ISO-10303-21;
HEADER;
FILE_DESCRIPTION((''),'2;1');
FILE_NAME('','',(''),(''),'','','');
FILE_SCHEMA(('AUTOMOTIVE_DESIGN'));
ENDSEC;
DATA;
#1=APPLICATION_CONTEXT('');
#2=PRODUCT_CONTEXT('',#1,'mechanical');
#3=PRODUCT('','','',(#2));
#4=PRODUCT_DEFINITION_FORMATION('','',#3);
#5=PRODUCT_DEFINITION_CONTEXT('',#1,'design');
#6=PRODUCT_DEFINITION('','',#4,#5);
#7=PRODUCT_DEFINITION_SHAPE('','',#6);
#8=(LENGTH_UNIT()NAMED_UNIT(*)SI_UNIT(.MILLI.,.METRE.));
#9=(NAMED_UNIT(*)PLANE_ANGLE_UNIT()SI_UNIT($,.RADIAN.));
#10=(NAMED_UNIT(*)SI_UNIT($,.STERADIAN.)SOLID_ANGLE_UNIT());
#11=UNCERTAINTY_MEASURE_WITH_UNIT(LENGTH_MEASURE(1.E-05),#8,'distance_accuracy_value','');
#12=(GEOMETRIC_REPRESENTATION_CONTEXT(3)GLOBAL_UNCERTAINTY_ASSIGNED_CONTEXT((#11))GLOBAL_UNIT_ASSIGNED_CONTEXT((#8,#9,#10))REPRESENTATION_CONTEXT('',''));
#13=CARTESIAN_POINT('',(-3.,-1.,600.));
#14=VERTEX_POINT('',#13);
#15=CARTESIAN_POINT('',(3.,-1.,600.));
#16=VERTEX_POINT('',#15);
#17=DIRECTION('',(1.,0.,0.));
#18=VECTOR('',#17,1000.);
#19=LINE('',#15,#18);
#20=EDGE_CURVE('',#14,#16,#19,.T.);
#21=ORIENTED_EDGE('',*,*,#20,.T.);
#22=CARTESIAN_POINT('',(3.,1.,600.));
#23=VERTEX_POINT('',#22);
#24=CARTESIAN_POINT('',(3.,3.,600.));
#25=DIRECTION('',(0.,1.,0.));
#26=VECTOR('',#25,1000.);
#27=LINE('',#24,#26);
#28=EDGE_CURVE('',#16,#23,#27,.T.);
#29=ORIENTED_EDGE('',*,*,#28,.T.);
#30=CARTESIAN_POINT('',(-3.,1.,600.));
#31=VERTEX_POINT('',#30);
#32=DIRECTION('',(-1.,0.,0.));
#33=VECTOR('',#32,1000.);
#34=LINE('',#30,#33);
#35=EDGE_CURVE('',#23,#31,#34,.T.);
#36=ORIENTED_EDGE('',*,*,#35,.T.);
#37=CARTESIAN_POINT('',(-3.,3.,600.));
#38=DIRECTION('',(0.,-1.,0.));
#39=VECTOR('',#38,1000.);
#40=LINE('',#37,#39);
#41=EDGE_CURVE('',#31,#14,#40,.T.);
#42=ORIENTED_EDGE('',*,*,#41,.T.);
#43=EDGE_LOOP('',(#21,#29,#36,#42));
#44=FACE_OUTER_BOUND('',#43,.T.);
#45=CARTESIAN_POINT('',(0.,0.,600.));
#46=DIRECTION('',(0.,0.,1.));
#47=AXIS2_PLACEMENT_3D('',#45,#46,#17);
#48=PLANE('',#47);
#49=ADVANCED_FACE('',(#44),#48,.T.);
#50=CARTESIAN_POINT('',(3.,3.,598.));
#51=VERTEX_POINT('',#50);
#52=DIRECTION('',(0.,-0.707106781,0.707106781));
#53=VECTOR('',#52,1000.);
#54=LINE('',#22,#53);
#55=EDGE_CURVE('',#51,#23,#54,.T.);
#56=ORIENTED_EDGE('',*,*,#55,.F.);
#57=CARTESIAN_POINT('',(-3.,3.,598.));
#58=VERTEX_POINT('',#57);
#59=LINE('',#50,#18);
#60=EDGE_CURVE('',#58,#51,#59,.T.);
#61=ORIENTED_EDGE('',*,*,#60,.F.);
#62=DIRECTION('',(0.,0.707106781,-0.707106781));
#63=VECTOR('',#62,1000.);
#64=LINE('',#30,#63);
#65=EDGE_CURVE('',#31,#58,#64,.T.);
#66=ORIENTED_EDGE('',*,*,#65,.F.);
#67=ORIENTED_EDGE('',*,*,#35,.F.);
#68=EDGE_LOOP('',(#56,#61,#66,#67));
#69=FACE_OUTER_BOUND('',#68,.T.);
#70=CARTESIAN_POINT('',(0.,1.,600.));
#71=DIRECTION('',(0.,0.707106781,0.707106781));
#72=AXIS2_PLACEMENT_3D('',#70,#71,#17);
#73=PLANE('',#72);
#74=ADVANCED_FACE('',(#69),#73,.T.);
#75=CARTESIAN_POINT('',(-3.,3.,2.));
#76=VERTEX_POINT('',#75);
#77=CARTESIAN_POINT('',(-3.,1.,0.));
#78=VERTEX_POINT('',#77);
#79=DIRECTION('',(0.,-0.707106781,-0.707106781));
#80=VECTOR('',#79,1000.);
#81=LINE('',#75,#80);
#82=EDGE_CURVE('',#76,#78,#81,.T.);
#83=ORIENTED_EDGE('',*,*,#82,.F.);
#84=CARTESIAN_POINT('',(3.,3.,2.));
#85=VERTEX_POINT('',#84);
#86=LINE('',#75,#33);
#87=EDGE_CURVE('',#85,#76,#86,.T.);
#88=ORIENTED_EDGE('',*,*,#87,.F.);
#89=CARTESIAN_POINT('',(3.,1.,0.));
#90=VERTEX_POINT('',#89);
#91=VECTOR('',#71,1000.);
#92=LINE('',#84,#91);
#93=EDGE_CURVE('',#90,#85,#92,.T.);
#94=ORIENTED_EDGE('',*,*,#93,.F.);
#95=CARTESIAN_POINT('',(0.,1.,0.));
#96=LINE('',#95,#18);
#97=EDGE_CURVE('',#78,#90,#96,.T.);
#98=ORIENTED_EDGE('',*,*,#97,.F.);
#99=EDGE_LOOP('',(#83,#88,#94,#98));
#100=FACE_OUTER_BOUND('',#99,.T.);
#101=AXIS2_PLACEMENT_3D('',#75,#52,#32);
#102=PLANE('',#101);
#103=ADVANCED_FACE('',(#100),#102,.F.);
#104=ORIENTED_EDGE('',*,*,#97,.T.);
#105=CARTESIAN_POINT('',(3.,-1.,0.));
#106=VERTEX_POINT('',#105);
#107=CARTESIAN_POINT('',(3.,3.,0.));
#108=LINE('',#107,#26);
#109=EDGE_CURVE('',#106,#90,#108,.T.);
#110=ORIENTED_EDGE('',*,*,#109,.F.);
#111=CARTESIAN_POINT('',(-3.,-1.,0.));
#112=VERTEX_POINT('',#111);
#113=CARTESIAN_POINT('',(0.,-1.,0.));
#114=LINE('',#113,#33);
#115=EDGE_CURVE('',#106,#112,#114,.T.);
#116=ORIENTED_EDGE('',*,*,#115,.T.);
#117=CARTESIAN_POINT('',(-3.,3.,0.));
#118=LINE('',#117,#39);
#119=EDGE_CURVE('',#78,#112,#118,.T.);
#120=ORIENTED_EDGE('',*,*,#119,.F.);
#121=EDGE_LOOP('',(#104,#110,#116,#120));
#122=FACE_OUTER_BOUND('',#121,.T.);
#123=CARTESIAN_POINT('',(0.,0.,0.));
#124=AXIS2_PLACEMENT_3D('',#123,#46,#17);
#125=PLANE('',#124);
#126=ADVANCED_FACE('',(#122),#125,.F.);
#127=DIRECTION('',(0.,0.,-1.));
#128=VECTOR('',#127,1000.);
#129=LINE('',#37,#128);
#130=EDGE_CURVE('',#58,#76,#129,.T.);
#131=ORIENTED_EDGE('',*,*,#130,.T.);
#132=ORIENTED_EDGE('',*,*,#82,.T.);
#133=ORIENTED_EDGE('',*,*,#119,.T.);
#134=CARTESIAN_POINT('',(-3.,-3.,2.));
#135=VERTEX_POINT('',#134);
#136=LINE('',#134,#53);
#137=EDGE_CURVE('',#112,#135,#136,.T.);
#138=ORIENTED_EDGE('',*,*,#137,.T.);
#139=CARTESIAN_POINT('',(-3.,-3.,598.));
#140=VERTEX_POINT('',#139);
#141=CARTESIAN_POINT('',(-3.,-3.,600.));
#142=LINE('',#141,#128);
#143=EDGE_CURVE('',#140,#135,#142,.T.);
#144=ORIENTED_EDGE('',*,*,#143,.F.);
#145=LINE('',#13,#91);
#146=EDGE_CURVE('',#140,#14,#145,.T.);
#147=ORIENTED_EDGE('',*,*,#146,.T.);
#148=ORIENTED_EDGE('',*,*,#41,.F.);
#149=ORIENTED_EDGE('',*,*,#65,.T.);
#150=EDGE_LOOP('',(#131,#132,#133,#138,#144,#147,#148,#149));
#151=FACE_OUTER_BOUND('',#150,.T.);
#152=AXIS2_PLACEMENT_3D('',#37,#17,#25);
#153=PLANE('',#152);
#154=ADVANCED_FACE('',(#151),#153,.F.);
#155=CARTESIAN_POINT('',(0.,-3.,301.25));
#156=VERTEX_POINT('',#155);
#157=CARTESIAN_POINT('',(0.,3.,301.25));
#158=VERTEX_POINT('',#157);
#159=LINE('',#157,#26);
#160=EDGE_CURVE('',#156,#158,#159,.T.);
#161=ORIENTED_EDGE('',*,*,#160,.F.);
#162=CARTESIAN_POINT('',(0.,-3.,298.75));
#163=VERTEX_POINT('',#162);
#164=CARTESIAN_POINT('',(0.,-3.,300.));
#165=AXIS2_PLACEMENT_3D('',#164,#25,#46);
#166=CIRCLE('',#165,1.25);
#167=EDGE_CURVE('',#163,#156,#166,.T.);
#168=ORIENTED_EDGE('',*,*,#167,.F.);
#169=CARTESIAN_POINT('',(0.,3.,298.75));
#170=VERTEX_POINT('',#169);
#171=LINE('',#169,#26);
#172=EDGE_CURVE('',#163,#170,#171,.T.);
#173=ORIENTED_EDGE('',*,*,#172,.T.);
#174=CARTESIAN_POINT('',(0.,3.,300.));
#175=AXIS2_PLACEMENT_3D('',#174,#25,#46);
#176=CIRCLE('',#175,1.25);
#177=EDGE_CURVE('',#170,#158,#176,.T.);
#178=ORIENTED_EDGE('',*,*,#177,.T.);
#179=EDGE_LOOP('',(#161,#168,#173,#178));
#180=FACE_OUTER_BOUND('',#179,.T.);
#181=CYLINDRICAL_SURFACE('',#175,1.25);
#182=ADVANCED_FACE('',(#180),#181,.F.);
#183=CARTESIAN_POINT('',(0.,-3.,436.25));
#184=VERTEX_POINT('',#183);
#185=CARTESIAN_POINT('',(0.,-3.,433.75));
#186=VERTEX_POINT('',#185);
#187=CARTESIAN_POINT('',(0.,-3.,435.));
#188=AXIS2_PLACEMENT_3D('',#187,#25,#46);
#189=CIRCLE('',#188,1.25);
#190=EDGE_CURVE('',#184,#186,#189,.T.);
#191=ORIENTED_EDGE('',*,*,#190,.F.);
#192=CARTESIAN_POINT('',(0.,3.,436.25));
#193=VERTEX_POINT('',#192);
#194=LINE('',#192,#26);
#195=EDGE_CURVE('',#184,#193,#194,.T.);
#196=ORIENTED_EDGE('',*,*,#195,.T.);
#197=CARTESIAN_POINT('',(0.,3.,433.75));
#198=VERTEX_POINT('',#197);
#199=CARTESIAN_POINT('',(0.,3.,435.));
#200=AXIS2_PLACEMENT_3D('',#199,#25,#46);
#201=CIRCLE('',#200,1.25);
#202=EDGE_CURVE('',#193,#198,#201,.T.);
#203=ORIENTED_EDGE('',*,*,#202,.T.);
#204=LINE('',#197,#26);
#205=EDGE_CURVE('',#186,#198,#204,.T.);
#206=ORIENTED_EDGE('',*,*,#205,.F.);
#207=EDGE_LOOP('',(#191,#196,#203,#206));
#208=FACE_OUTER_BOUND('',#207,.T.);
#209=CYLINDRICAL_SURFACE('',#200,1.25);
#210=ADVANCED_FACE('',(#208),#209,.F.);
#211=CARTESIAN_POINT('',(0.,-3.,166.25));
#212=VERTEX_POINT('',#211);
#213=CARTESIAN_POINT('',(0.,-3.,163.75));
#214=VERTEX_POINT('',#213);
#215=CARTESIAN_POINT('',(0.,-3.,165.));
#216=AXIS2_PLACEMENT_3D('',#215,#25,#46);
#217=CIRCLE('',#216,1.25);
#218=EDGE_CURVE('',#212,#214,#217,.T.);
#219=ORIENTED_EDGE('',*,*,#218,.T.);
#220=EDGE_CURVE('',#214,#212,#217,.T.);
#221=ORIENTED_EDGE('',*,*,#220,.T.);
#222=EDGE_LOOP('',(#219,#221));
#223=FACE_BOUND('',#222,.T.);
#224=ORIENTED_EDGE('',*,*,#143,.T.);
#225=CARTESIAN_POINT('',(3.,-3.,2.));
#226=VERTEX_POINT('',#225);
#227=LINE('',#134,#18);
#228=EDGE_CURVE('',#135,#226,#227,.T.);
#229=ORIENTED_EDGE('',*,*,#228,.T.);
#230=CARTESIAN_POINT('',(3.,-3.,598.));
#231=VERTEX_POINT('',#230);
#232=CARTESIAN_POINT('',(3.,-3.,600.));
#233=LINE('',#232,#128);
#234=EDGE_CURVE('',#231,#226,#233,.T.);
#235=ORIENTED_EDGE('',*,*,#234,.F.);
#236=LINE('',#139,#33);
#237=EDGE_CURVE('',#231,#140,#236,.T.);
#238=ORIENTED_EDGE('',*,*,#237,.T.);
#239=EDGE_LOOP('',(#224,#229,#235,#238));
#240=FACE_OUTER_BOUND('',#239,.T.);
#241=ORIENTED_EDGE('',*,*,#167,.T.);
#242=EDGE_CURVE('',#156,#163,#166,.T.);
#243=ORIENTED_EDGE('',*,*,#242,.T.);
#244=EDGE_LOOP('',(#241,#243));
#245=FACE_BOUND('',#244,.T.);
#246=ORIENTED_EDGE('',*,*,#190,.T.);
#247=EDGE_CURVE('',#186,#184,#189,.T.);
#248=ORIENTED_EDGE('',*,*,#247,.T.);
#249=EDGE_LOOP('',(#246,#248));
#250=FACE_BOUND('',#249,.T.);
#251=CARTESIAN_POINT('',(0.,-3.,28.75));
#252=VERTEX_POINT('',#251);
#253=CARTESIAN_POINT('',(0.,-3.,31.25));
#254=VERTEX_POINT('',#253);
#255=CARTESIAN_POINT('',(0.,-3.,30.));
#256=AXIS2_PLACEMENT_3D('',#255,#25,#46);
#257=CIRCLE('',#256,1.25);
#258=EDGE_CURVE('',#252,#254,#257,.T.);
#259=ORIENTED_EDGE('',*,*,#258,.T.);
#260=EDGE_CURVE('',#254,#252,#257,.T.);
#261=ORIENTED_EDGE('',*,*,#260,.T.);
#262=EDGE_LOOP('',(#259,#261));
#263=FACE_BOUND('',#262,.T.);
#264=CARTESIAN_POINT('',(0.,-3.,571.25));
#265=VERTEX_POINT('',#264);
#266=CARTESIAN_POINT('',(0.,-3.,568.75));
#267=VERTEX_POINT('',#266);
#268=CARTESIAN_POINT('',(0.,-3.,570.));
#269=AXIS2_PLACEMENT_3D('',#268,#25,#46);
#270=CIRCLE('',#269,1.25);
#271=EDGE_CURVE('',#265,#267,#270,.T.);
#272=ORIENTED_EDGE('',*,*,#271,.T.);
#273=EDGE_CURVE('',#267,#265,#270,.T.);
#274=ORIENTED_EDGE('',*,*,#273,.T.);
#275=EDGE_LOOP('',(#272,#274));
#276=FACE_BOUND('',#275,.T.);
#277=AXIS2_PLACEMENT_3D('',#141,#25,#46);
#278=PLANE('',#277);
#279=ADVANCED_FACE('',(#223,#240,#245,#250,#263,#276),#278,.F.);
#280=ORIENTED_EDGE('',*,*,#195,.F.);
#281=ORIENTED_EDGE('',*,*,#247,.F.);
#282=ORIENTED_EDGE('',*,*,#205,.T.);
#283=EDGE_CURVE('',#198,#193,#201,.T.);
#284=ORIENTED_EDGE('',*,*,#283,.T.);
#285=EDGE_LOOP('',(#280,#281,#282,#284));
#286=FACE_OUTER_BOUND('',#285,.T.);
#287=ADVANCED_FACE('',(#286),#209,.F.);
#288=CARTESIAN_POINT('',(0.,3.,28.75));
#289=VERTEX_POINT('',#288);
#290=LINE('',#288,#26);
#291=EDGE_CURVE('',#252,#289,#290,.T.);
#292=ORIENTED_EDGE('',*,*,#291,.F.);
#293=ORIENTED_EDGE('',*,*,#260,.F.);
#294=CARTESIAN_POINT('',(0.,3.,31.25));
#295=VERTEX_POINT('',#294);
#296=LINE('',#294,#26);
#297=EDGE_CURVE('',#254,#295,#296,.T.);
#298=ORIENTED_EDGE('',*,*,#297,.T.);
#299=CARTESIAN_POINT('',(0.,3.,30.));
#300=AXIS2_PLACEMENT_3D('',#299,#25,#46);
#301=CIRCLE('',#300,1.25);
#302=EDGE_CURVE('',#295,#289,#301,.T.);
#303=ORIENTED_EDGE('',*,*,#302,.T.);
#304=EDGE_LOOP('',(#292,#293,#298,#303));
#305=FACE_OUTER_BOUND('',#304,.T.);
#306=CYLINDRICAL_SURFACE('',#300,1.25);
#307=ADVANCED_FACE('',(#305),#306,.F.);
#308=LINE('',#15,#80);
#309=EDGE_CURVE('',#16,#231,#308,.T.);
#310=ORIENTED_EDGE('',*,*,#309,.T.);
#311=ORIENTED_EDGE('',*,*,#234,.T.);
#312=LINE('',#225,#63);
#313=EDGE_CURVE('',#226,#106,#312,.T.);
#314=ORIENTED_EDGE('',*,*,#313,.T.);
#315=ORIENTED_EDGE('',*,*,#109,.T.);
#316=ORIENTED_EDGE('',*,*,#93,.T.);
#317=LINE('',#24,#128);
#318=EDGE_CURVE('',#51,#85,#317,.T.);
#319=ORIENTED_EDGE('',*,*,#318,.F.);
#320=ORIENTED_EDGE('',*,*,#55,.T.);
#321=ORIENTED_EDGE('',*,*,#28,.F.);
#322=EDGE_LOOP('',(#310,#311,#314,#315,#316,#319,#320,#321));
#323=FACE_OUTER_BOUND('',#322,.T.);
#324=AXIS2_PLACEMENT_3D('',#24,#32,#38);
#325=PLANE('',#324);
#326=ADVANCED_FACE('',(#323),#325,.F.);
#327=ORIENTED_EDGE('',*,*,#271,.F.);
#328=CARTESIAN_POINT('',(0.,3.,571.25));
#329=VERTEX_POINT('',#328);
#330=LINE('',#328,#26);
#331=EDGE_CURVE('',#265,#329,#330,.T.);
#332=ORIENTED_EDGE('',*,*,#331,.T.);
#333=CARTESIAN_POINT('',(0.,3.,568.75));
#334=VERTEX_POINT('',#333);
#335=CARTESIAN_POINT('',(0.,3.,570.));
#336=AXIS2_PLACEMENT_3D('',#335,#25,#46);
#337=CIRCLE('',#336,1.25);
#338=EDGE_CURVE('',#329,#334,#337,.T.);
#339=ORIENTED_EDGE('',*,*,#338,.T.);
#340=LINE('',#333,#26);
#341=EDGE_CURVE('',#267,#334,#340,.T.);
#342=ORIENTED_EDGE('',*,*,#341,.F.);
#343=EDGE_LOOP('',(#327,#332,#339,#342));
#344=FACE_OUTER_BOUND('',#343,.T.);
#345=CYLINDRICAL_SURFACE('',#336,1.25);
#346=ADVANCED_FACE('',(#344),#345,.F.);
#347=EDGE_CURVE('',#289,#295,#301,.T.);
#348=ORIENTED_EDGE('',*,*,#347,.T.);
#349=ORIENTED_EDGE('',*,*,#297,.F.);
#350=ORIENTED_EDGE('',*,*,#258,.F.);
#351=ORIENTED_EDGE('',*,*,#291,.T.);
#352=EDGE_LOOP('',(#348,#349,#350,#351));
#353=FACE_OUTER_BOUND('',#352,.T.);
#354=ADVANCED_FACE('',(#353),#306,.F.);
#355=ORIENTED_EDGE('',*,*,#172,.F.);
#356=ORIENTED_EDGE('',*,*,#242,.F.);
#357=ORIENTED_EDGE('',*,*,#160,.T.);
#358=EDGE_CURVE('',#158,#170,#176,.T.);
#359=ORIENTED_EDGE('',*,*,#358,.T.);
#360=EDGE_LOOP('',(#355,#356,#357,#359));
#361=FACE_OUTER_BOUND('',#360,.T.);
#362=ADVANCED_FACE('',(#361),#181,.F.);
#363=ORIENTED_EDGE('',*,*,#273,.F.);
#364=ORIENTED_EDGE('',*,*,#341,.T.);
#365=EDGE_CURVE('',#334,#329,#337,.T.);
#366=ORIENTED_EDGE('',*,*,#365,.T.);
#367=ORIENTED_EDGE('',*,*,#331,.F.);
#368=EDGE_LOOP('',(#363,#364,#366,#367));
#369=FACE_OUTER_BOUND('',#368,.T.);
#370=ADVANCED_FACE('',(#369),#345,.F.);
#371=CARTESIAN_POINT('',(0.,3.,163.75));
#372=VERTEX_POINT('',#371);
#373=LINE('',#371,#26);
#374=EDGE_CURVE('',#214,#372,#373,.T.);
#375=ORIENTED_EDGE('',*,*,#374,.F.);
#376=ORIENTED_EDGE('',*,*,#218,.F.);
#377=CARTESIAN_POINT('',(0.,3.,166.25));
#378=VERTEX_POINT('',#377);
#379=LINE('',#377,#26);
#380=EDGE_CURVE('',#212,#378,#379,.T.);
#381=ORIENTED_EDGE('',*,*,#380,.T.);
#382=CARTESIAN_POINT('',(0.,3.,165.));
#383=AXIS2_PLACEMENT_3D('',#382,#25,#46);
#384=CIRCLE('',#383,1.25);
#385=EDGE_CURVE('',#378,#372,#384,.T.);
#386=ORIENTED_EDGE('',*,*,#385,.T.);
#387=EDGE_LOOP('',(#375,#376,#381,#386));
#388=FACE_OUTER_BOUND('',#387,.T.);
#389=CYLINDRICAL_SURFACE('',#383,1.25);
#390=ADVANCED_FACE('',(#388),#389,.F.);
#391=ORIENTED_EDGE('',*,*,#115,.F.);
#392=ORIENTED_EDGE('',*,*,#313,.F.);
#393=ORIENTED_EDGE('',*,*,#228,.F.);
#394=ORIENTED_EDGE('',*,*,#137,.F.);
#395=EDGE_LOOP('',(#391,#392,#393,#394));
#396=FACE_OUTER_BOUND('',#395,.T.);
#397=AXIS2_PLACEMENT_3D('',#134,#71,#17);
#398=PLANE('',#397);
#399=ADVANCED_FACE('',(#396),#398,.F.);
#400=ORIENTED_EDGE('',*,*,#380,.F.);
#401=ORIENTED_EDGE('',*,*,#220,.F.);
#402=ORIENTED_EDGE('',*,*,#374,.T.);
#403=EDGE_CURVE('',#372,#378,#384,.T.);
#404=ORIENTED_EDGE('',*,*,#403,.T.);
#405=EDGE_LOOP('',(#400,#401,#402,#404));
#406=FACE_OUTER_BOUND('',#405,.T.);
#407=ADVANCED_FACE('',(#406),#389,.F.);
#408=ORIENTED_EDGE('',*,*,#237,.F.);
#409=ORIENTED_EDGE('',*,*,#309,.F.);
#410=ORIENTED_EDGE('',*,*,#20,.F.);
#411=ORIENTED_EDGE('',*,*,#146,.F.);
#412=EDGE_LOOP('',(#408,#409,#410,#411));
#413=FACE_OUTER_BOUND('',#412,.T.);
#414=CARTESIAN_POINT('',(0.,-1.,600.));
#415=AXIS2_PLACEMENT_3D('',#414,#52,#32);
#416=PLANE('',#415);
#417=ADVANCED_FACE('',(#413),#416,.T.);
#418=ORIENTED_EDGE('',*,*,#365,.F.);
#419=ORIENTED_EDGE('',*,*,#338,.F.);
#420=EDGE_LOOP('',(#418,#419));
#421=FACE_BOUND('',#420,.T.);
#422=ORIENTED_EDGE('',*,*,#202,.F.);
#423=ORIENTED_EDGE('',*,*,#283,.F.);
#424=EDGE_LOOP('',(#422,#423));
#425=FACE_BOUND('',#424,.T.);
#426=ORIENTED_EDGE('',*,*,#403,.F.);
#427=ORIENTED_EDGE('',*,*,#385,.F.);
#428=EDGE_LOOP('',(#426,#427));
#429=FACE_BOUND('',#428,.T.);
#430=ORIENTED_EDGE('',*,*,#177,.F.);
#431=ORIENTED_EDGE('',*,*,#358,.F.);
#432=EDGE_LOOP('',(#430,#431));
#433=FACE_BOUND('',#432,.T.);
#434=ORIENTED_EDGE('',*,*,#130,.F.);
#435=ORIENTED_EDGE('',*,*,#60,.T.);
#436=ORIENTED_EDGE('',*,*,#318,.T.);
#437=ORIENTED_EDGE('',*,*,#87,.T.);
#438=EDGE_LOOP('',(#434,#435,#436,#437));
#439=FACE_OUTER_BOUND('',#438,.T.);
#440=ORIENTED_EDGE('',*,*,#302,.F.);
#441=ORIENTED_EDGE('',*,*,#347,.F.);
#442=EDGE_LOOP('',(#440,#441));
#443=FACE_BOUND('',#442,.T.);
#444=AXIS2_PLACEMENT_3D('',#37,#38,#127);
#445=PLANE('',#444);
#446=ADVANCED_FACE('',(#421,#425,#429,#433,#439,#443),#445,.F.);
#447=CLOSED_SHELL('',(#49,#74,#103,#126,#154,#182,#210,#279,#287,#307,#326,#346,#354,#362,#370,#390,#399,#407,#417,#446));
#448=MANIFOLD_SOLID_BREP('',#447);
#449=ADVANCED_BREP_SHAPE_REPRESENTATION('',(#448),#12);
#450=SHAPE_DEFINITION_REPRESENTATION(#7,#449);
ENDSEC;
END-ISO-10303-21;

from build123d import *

# Parameters (mm, degrees)
SKETCH_1_W         = 6
SKETCH_1_H         = 6
EXTRUDE_1_DEPTH    = 600
HOLE_WIZARD_M3_1_D = 2.5
CHAMFER_1_SIZE     = 2


with BuildPart() as part:
    # 草图1 → 凸台-拉伸1 (new body)
    with BuildSketch(Plane.XY):
        Rectangle(SKETCH_1_W, SKETCH_1_H)
    extrude(amount=EXTRUDE_1_DEPTH)

    # M3 螺纹孔1 (through all)
    with Locations(Plane(origin=(0, 3, 165), x_dir=(0, 0, 1), z_dir=(0, 1, 0))):
        with Locations((0, 0), (135, 0), (270, 0), (405, 0), (-135, 0)):
            Hole(HOLE_WIZARD_M3_1_D / 2)

    # 倒角1
    chamfer_1_edges = [part.edges().sort_by_distance(p)[0] for p in [
        (0, -3, 600),
        (0, -3, 0),
        (0, 3, 0),
        (0, 3, 600),
    ]]
    chamfer(chamfer_1_edges, length=CHAMFER_1_SIZE)


solid = part.part
